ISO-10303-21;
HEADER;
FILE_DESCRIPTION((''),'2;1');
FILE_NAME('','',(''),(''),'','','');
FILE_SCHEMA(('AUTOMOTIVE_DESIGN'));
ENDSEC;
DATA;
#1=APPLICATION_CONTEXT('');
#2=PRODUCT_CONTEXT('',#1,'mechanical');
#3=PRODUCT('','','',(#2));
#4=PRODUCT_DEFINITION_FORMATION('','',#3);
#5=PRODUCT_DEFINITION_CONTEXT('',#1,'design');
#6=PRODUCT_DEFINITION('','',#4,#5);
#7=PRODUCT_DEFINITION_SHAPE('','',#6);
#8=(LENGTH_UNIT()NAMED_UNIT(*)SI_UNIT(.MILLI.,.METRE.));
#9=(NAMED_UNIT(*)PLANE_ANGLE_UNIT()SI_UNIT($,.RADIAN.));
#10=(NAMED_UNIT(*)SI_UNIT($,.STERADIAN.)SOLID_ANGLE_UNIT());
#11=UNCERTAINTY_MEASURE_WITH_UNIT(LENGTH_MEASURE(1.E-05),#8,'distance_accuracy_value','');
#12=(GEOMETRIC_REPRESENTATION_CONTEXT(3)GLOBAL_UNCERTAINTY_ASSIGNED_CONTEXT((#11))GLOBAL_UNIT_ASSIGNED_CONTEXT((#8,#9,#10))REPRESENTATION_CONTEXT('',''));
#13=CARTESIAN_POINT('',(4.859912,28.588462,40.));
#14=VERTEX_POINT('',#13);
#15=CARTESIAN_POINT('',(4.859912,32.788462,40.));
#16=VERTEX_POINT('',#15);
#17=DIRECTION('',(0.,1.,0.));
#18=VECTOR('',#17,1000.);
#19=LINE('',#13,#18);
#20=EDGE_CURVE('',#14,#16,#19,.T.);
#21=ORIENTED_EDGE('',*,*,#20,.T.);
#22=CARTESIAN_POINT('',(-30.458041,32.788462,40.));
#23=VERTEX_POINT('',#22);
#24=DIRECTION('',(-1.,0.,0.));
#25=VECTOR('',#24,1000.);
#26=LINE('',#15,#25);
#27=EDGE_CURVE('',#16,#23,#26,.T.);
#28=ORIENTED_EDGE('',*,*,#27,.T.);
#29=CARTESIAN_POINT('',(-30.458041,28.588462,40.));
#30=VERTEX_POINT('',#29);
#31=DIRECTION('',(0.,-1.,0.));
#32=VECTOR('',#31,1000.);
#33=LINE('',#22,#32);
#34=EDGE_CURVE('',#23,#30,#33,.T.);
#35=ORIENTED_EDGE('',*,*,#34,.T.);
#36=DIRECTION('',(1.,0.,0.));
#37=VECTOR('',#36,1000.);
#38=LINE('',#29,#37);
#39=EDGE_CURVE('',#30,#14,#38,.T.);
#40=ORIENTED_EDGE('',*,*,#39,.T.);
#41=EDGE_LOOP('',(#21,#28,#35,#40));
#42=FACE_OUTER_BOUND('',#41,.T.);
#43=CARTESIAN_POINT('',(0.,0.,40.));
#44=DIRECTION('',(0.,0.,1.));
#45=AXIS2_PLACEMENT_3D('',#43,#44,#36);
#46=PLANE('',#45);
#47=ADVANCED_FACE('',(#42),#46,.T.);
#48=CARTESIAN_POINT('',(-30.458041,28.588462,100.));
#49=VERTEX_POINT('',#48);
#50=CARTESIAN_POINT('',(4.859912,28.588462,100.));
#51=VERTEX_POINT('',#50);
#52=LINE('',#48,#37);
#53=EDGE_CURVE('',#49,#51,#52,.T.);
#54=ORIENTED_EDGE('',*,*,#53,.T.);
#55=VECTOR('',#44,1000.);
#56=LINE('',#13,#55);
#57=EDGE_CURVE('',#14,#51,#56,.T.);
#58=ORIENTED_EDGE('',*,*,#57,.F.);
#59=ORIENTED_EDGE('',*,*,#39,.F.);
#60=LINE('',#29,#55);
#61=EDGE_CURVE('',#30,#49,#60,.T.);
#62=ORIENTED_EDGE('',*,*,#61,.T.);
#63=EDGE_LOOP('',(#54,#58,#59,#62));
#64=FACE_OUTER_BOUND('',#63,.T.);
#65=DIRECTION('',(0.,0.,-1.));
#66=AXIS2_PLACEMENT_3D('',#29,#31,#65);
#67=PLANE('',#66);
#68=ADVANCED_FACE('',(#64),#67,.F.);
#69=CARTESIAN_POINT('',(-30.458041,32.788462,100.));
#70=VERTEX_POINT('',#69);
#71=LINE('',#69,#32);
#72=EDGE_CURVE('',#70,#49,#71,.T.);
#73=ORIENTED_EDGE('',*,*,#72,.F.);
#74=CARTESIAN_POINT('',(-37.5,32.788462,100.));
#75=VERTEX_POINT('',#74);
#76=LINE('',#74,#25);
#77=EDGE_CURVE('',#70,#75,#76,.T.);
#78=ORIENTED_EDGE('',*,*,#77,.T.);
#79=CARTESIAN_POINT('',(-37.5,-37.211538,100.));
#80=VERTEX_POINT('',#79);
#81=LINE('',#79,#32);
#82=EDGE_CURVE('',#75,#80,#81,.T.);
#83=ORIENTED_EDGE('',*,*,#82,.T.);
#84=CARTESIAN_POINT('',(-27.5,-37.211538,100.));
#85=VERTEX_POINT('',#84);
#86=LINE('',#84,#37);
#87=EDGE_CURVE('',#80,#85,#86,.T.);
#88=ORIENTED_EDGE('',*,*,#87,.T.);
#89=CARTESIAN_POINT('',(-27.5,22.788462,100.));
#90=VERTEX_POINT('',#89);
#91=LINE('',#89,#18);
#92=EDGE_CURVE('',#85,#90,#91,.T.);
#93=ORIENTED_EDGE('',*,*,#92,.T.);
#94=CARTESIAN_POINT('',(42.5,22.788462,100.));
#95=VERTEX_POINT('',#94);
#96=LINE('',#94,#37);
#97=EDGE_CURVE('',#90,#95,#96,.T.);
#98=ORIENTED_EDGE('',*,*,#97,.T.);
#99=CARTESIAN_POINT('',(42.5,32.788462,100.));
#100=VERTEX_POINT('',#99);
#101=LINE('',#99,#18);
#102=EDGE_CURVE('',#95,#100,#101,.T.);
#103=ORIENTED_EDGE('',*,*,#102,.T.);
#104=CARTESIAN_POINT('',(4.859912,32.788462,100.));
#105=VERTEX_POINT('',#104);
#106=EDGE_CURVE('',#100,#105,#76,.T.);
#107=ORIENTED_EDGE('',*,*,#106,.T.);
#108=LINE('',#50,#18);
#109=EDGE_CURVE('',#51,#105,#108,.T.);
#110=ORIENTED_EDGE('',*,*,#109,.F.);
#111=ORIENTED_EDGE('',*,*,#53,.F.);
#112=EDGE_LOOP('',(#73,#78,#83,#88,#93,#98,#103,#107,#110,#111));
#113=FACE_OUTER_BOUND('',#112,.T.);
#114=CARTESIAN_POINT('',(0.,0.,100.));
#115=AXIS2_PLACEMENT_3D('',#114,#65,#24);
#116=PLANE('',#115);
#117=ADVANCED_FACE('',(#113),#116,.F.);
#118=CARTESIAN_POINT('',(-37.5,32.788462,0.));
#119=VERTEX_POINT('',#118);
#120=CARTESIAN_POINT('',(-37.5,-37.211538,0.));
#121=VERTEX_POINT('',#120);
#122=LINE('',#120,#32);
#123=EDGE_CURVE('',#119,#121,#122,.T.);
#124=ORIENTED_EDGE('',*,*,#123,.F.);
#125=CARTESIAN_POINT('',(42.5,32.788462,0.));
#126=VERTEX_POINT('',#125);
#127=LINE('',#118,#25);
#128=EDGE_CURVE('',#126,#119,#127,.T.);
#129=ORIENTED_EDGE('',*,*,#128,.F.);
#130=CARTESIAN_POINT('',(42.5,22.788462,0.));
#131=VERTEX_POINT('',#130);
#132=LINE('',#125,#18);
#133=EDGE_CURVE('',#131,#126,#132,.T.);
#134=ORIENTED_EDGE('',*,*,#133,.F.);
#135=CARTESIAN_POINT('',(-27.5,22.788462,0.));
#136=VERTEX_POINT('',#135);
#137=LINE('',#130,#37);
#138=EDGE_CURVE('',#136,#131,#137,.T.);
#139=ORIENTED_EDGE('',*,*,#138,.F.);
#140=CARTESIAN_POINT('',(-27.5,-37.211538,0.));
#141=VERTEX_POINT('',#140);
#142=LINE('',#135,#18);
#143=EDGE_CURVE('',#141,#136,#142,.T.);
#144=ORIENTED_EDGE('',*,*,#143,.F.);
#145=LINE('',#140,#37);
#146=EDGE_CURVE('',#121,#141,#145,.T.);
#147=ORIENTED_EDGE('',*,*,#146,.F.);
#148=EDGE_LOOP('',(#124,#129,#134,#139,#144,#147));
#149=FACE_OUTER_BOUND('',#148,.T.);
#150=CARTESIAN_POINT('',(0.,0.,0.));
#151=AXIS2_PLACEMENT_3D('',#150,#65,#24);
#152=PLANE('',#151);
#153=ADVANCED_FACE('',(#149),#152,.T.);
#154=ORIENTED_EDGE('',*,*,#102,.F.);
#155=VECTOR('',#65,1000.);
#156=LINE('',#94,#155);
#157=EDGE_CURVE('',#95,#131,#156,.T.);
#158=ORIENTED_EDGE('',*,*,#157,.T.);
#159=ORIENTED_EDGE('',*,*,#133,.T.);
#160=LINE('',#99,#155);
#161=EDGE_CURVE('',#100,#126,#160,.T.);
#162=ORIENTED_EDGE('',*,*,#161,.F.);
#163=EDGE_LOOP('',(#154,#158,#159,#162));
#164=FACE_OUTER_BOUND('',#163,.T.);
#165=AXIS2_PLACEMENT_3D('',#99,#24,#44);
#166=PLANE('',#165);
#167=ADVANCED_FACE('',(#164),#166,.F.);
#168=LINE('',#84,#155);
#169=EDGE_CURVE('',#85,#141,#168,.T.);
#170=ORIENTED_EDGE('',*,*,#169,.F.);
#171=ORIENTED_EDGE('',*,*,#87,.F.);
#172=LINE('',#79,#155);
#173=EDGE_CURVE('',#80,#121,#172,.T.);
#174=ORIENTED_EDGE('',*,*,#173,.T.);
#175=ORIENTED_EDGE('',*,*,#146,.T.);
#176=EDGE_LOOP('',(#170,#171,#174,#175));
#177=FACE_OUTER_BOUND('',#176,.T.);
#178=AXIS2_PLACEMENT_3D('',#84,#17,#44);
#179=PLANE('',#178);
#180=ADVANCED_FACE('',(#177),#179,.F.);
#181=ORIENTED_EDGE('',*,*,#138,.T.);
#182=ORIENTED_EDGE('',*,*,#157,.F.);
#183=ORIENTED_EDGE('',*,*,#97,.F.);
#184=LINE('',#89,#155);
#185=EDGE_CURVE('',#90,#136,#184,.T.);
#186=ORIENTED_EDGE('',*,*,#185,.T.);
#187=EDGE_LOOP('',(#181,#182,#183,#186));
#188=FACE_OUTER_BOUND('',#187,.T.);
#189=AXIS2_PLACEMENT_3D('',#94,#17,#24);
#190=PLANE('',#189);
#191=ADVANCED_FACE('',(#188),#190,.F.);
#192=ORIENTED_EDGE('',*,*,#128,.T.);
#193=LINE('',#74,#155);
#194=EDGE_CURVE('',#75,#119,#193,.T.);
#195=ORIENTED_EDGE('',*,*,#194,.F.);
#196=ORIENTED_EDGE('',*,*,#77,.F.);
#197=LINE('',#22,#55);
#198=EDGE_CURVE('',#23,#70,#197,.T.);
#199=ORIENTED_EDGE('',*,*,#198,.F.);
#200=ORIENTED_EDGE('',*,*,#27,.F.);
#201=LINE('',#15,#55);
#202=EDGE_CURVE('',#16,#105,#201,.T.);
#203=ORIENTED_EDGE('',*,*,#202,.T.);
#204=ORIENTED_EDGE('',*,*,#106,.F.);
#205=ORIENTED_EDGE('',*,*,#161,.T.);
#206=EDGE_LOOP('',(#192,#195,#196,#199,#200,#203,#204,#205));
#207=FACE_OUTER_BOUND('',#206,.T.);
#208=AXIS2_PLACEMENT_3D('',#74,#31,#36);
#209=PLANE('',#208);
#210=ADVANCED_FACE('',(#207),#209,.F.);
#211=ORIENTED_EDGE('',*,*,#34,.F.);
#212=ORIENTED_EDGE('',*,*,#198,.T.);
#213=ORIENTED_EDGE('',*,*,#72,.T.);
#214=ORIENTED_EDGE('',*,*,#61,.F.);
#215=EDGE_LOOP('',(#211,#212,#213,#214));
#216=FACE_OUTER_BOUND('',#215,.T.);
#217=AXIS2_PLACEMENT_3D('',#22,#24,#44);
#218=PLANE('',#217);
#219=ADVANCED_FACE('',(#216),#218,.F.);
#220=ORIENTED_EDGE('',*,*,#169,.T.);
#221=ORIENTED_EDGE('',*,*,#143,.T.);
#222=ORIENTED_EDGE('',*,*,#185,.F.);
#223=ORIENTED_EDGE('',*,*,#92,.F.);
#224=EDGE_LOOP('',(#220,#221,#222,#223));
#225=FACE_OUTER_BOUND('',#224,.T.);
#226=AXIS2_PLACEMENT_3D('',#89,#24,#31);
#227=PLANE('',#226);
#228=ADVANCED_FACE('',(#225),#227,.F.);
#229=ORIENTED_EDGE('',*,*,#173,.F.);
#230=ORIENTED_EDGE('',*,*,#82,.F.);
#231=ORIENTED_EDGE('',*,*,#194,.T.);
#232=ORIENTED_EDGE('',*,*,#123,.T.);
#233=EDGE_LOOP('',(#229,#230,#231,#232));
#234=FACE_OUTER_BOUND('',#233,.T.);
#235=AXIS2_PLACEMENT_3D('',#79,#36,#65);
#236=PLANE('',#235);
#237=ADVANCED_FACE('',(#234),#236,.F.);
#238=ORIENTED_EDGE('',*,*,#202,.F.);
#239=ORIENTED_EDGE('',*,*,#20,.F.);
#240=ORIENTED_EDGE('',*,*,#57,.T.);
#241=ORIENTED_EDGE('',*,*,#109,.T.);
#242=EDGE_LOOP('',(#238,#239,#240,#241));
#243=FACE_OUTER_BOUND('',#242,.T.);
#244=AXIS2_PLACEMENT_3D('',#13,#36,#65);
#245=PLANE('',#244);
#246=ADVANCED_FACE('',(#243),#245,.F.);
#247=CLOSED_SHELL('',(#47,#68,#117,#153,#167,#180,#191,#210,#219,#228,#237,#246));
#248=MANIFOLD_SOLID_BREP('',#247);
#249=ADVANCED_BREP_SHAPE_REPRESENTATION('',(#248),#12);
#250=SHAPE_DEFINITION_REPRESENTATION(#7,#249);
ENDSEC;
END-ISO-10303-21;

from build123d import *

# Parameters (mm, degrees)
EXTRUDE_1_DEPTH     = 100
SKETCH_2_W          = 35.317953013
SKETCH_2_H          = 4.2
CUT_EXTRUDE_1_DEPTH = 60


with BuildPart() as part:
    # 草图1 → 凸台-拉伸1 (new body)
    with BuildSketch(Plane.XY):
        Polygon((-37.5, 32.788461538), (42.5, 32.788461538), (42.5, 22.788461538), (-27.5, 22.788461538), (-27.5, -37.211538462), (-37.5, -37.211538462), align=None)
    extrude(amount=EXTRUDE_1_DEPTH)

    # 草图2 → 切除-拉伸1 (cut)
    with BuildSketch(Plane.XY.offset(100)):
        with Locations((-12.799064643, 30.688461538)):
            Rectangle(SKETCH_2_W, SKETCH_2_H)
    extrude(amount=-CUT_EXTRUDE_1_DEPTH, mode=Mode.SUBTRACT)


solid = part.part
